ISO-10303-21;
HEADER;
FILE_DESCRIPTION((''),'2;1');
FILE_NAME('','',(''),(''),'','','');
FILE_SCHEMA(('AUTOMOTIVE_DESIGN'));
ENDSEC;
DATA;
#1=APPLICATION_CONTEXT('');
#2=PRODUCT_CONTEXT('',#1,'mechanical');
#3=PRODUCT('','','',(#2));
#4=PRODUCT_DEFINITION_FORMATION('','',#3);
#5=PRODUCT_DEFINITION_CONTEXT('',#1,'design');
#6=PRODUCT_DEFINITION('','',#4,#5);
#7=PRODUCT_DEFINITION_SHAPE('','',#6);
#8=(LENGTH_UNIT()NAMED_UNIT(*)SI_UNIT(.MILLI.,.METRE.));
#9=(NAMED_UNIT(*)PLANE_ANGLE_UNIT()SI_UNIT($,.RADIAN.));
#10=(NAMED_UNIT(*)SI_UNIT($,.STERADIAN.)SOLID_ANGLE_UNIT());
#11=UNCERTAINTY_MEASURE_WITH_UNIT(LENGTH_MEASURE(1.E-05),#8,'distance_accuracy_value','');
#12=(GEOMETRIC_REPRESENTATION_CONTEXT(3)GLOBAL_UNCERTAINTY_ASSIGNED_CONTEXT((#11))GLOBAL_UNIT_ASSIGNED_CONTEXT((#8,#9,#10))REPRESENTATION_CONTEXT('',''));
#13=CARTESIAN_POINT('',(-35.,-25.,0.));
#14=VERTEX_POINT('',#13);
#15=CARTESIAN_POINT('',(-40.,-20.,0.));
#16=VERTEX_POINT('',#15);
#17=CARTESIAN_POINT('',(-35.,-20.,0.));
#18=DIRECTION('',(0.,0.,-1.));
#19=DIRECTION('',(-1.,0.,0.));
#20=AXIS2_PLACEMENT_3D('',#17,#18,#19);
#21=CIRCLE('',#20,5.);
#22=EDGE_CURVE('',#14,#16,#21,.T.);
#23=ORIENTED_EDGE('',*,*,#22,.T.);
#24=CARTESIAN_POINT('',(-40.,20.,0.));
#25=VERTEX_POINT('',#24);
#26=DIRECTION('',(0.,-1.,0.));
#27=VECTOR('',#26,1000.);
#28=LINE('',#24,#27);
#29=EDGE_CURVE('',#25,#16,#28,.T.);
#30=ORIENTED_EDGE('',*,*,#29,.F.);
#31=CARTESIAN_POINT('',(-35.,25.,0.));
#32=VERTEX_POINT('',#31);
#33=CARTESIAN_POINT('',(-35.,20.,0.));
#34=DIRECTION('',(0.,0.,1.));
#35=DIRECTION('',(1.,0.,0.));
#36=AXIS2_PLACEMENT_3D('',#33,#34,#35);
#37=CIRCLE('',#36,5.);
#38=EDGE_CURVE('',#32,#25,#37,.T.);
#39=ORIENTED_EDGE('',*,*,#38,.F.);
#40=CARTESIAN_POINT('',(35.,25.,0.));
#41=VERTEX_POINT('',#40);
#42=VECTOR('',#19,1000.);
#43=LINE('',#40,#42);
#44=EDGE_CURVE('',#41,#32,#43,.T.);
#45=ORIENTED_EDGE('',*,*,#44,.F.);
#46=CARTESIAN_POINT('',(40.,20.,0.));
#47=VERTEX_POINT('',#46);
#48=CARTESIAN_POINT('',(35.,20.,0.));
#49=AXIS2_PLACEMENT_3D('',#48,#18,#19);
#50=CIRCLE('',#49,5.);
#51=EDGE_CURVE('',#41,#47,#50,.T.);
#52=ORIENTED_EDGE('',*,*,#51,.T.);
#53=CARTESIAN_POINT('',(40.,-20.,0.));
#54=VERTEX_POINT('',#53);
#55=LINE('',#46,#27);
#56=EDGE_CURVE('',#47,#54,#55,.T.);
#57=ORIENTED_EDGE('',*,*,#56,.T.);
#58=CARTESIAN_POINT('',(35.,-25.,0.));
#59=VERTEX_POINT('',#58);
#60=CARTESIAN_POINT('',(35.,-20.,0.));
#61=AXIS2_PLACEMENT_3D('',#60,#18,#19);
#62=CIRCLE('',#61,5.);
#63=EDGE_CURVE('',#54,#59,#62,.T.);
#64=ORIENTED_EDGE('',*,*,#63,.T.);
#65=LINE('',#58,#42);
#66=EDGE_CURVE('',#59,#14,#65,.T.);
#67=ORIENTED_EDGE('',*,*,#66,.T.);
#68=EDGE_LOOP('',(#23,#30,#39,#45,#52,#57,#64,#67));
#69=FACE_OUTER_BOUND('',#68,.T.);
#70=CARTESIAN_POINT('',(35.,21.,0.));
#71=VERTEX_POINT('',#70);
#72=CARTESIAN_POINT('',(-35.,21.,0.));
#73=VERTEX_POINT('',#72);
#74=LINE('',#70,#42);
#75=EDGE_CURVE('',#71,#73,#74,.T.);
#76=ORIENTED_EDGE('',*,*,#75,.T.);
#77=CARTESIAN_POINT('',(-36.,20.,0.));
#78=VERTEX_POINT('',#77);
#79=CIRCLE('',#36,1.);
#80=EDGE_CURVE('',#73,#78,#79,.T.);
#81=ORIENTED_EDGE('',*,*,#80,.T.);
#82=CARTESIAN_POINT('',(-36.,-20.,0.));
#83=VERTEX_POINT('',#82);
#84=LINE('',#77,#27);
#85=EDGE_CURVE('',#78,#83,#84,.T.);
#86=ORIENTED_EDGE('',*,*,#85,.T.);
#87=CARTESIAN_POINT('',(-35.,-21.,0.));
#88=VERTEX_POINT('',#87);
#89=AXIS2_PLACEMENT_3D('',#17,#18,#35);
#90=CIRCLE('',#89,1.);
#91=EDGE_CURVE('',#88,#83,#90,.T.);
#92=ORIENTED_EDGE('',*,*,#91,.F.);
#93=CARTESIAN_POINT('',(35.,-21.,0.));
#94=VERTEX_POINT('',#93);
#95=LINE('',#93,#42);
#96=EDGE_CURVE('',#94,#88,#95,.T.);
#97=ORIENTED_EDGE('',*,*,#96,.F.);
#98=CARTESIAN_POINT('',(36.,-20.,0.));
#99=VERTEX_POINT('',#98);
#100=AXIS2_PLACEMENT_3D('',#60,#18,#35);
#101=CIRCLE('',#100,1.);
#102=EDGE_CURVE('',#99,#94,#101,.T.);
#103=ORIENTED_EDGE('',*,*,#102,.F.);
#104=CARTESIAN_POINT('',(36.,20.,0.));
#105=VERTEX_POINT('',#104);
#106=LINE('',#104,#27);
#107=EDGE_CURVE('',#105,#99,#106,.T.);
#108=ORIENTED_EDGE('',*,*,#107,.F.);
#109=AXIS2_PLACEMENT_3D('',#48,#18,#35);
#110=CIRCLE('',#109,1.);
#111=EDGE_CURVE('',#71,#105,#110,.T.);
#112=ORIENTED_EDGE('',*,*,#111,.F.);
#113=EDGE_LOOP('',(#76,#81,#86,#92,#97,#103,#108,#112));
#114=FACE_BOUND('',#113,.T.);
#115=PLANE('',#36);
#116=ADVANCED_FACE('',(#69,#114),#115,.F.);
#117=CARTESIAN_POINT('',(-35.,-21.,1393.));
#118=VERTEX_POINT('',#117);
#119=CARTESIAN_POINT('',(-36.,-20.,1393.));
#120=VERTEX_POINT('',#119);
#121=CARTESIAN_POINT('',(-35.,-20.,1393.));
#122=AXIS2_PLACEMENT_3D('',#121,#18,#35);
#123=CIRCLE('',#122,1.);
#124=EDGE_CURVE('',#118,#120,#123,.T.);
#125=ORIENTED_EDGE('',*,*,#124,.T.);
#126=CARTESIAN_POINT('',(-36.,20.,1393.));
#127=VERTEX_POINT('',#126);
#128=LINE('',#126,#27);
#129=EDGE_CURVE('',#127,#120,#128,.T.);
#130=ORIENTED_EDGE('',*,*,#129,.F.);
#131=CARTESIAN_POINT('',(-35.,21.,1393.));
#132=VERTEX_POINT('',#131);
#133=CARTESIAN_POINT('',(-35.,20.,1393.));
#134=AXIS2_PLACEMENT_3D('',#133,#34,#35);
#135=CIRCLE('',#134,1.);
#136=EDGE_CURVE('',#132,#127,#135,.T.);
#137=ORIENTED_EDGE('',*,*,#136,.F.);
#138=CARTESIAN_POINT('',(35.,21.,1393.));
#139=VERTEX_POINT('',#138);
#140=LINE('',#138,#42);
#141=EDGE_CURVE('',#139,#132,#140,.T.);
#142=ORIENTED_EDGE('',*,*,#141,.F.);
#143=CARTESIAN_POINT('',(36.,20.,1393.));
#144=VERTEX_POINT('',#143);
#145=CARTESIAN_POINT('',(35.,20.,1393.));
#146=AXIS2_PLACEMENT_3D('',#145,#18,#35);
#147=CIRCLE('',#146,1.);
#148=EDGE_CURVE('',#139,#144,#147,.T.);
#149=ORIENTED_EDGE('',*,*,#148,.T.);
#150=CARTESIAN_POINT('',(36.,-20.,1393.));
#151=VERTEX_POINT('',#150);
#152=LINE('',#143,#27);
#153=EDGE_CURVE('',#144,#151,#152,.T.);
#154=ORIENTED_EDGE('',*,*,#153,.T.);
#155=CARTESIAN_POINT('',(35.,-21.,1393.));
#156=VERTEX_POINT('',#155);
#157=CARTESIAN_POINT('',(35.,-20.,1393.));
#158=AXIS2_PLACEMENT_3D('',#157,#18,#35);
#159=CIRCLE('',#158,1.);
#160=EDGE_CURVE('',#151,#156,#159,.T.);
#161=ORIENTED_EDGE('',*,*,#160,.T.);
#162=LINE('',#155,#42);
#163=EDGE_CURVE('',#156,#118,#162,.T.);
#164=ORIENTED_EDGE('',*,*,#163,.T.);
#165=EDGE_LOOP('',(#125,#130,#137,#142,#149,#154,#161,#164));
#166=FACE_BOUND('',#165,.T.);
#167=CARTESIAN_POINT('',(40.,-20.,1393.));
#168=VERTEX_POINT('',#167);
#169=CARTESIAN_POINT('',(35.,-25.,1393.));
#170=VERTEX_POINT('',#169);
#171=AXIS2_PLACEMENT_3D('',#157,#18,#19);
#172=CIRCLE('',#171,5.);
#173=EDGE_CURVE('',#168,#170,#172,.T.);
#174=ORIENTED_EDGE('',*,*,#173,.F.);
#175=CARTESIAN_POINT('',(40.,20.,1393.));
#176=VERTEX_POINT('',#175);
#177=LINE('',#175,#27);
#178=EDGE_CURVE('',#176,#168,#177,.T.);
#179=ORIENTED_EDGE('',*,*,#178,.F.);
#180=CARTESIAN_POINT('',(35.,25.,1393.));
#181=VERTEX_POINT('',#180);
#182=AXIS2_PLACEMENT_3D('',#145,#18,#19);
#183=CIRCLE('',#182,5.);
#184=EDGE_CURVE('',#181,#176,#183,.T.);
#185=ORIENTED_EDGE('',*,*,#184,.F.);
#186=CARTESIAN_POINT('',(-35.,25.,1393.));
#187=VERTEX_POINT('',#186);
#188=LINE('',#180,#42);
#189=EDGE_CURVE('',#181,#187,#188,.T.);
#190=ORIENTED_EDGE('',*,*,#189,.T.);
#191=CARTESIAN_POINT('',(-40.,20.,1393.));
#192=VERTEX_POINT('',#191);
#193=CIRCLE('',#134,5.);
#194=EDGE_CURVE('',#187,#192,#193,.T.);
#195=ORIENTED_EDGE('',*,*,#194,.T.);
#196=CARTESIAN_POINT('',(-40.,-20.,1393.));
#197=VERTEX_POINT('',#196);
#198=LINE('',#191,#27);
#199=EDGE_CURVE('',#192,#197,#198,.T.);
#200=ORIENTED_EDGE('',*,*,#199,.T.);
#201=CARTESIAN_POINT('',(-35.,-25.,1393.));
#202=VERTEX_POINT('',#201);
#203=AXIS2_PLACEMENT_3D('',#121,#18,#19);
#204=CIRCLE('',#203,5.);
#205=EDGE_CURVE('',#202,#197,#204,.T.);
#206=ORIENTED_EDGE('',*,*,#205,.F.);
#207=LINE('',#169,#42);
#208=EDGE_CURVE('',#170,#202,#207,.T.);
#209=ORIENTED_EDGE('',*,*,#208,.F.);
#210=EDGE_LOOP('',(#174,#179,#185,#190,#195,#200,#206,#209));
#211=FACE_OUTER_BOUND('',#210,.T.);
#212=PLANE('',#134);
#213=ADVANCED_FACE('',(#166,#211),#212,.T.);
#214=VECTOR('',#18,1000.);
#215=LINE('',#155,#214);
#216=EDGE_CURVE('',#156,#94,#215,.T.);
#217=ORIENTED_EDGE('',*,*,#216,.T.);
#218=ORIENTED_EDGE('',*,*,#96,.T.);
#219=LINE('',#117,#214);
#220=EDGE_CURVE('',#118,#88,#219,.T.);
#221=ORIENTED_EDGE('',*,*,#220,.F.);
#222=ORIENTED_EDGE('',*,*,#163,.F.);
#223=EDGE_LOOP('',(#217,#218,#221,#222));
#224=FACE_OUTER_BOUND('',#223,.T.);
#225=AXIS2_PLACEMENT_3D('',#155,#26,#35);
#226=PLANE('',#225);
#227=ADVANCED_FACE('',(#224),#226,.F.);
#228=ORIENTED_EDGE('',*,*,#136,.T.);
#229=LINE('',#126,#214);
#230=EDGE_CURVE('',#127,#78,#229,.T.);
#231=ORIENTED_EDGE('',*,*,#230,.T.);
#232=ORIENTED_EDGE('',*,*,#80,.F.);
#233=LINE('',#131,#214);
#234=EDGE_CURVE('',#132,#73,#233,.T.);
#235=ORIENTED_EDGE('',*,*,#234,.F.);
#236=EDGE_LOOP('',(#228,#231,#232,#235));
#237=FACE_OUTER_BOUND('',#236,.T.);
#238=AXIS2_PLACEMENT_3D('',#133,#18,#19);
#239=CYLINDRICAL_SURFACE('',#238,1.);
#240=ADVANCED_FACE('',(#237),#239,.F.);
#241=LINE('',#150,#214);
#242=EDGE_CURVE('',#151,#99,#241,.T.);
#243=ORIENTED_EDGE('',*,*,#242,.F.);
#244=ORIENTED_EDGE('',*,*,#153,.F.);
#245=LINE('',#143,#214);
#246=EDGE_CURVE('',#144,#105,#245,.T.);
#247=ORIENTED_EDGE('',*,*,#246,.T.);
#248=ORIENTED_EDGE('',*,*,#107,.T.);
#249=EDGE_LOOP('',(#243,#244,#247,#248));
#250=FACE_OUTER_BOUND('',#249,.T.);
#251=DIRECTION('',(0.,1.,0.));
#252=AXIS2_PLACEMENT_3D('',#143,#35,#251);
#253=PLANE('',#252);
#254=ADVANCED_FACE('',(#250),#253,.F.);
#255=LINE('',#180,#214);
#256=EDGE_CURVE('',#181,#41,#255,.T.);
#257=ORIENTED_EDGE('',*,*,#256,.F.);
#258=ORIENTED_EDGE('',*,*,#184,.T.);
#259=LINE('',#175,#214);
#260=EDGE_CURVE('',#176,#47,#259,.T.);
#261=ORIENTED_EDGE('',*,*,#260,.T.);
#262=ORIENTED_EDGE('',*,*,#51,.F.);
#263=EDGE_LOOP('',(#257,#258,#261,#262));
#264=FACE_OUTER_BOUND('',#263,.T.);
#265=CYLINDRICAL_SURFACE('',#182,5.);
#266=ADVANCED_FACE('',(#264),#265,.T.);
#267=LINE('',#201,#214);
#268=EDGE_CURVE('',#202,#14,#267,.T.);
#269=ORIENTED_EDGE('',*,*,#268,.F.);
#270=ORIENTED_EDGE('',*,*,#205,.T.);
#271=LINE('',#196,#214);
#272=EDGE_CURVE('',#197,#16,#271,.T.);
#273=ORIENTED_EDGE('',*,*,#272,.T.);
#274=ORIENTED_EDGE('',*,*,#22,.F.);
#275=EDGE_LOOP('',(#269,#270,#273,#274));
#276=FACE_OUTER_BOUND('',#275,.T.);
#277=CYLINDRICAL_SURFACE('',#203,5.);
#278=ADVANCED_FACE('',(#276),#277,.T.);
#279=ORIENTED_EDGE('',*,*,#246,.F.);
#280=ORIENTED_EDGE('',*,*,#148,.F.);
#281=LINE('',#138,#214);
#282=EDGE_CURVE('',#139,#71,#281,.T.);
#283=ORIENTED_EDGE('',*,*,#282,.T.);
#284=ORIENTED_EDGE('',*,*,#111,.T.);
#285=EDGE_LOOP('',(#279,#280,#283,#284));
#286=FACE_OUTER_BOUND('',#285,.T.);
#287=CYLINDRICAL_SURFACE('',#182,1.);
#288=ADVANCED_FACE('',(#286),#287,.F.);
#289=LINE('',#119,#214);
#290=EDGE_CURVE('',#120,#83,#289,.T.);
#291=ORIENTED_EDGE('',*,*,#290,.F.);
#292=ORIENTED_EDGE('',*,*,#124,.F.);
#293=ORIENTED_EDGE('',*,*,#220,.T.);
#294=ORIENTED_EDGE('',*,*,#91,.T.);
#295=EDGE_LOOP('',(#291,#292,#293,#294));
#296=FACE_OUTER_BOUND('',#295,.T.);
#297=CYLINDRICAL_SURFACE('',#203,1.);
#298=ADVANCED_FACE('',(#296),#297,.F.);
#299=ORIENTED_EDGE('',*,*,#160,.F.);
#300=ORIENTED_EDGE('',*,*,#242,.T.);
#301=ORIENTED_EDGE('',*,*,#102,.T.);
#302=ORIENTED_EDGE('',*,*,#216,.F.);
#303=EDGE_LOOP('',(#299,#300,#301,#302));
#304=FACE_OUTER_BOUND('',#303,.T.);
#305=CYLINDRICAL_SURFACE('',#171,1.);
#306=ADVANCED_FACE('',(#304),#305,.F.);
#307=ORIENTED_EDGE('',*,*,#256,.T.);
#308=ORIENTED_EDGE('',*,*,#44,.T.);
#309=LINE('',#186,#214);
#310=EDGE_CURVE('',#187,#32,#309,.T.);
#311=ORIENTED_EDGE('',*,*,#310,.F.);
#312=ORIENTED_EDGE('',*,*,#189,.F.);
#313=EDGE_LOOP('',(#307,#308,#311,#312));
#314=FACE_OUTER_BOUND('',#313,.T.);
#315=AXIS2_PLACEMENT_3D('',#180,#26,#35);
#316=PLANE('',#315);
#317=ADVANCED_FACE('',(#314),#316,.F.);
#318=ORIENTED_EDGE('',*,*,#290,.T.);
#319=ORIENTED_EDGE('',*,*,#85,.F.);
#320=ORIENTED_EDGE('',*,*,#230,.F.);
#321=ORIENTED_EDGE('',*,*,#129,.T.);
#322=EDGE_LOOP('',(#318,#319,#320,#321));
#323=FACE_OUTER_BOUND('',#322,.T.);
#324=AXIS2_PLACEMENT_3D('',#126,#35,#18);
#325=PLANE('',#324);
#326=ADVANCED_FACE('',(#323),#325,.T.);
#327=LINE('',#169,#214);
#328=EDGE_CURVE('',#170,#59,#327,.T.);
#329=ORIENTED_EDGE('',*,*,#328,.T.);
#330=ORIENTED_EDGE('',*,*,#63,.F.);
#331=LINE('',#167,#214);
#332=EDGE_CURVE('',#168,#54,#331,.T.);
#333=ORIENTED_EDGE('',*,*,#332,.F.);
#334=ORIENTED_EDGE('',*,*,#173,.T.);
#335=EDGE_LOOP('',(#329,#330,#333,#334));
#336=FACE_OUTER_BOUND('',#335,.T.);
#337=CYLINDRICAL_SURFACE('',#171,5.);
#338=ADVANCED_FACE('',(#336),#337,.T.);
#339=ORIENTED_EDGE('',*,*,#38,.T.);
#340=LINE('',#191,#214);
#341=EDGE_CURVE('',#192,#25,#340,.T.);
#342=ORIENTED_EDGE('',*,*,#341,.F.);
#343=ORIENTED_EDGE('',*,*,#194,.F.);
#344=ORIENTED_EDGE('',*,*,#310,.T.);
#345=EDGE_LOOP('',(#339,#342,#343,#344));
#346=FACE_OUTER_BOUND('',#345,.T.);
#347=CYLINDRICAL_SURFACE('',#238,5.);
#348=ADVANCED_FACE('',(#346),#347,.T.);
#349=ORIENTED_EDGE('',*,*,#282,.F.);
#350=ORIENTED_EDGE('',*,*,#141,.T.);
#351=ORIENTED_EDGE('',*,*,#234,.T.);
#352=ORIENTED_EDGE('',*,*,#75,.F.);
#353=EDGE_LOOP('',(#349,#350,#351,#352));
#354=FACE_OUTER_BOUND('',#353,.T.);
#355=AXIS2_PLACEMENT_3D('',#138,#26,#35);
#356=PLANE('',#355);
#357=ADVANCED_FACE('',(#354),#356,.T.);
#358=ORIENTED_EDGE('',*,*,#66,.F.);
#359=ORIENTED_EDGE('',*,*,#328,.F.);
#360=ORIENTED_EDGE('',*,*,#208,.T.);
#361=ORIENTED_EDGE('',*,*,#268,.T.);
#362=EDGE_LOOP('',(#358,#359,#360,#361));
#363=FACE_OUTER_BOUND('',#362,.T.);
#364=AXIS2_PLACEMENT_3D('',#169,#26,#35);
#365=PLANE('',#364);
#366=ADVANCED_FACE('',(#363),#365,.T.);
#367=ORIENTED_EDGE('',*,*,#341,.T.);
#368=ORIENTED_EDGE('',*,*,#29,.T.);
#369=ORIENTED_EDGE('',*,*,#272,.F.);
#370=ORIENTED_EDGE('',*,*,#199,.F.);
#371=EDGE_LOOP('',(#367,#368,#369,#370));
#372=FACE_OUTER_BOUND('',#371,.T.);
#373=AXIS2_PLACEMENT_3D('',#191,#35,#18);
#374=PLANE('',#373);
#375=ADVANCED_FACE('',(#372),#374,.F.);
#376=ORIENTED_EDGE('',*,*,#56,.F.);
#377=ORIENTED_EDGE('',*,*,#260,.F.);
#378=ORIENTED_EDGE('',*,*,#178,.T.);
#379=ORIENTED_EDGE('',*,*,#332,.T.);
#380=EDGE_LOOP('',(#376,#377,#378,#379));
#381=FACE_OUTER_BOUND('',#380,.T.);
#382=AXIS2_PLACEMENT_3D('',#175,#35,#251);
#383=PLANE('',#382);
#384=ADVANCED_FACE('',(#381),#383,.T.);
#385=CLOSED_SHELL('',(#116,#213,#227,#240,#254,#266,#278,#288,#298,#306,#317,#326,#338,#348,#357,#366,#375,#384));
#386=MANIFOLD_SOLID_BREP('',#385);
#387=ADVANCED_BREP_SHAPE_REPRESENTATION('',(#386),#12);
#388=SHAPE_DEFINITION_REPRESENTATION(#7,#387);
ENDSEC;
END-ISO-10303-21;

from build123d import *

# Parameters (mm, degrees)
BOSS_EXTRUDE1_DEPTH = 1393
SHELL1_T            = -4


with BuildPart() as part:
    # Sketch1 → Boss-Extrude1 (new body)
    with BuildSketch(Plane.XY):
        with BuildLine():
            Line((35, 25), (-35, 25))
            ThreePointArc((-35, 25), (-38.535533906, 23.535533906), (-40, 20))
            Line((-40, 20), (-40, -20))
            ThreePointArc((-40, -20), (-38.535533906, -23.535533906), (-35, -25))
            Line((-35, -25), (35, -25))
            ThreePointArc((35, -25), (38.535533906, -23.535533906), (40, -20))
            Line((40, -20), (40, 20))
            ThreePointArc((40, 20), (38.535533906, 23.535533906), (35, 25))
        make_face()
    extrude(amount=BOSS_EXTRUDE1_DEPTH)

    # Shell1
    shell1_openings = [part.faces().sort_by_distance(p)[0] for p in [
        (0, 0, 1393),
        (0, 0, 0),
    ]]
    offset(amount=SHELL1_T, openings=shell1_openings, kind=Kind.INTERSECTION)


solid = part.part
